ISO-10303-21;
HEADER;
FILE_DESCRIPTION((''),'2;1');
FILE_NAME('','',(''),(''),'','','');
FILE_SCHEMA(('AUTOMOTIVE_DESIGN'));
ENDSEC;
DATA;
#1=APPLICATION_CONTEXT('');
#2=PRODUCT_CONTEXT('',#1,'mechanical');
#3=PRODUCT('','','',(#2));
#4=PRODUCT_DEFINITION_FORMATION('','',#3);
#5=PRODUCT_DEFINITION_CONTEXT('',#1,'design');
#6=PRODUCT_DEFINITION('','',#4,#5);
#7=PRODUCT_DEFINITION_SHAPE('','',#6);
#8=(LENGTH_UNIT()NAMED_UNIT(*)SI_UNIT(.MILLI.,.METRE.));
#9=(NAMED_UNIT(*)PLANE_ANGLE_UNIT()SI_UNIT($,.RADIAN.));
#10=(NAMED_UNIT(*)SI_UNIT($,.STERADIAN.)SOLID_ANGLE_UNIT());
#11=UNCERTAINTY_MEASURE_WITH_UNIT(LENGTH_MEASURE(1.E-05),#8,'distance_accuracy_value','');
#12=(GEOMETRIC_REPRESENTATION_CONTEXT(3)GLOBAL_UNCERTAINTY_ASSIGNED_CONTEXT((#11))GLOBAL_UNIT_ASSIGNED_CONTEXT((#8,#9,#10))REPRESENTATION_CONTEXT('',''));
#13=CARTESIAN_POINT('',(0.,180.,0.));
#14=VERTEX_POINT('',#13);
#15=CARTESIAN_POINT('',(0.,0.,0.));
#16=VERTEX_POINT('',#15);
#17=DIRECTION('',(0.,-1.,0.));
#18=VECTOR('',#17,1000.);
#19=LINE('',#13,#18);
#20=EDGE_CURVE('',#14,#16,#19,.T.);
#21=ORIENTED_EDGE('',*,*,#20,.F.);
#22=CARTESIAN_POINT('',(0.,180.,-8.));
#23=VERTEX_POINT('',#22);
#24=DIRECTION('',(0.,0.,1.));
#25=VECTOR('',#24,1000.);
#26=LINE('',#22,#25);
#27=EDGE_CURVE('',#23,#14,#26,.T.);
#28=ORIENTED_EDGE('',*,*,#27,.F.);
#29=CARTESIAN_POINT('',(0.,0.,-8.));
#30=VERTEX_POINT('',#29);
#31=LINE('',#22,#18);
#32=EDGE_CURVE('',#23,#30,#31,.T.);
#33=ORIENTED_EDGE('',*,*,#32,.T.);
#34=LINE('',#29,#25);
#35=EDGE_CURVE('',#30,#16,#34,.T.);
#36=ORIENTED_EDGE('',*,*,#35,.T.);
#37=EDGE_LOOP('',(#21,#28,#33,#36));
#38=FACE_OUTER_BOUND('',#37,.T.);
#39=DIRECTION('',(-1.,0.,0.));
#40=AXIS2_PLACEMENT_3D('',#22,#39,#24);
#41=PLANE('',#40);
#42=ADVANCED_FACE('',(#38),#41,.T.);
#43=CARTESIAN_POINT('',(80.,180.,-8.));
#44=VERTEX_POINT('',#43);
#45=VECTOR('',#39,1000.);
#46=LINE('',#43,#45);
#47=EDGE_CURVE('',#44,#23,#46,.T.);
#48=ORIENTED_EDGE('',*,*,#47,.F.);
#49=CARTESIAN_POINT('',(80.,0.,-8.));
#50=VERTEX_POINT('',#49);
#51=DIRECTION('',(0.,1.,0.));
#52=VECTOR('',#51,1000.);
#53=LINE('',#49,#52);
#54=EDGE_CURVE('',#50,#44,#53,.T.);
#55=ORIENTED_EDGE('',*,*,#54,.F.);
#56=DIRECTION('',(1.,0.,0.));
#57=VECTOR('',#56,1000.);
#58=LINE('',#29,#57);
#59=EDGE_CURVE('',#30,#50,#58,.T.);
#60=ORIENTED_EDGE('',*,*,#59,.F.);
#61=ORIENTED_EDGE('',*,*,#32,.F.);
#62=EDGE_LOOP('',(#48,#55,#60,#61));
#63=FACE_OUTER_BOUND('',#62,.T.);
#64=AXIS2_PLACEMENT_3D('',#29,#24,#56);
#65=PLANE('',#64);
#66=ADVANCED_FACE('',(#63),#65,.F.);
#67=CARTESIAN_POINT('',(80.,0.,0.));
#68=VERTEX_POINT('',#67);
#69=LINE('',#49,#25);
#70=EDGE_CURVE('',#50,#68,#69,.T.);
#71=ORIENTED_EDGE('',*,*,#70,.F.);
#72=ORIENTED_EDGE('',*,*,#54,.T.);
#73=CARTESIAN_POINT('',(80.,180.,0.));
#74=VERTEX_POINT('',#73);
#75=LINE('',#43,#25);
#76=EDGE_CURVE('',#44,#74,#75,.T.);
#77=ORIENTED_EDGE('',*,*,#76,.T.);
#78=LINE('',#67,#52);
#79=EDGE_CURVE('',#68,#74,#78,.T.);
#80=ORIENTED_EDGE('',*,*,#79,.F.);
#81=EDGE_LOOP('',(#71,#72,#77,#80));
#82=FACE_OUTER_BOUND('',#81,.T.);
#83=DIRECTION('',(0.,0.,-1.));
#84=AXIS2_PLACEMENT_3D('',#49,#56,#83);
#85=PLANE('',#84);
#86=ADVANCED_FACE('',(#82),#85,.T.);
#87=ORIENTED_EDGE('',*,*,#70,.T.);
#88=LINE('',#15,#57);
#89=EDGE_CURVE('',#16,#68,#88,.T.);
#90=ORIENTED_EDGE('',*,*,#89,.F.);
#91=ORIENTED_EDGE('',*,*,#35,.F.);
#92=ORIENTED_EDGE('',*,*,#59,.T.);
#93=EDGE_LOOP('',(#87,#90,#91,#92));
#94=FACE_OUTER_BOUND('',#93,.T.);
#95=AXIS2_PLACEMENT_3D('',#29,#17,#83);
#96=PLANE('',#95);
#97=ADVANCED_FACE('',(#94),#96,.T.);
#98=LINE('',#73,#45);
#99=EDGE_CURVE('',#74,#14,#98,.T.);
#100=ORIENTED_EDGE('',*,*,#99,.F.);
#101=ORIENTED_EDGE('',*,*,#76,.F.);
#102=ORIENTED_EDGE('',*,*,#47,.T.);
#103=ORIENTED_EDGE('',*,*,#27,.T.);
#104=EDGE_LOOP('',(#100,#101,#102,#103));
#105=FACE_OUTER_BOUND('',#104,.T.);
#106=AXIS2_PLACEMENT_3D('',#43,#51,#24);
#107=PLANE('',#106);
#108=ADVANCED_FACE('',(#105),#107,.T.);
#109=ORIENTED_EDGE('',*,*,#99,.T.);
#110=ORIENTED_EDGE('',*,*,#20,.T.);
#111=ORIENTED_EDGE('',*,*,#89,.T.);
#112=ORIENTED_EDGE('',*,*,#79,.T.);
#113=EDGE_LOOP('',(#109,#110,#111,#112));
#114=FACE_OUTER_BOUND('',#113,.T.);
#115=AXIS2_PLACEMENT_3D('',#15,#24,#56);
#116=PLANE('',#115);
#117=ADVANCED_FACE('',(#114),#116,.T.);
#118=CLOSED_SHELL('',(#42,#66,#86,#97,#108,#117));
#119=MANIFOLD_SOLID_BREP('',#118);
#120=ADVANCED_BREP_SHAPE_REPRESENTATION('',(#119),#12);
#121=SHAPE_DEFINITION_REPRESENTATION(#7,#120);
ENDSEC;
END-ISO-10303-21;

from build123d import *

# Parameters (mm, degrees)
SKETCH_1_W      = 80
SKETCH_1_H      = 180
EXTRUDE_1_DEPTH = 8


with BuildPart() as part:
    # 草图1 → 凸台-拉伸1 (new body)
    with BuildSketch(Plane.XY):
        with Locations((40, 90)):
            Rectangle(SKETCH_1_W, SKETCH_1_H)
    extrude(amount=-EXTRUDE_1_DEPTH)


solid = part.part
